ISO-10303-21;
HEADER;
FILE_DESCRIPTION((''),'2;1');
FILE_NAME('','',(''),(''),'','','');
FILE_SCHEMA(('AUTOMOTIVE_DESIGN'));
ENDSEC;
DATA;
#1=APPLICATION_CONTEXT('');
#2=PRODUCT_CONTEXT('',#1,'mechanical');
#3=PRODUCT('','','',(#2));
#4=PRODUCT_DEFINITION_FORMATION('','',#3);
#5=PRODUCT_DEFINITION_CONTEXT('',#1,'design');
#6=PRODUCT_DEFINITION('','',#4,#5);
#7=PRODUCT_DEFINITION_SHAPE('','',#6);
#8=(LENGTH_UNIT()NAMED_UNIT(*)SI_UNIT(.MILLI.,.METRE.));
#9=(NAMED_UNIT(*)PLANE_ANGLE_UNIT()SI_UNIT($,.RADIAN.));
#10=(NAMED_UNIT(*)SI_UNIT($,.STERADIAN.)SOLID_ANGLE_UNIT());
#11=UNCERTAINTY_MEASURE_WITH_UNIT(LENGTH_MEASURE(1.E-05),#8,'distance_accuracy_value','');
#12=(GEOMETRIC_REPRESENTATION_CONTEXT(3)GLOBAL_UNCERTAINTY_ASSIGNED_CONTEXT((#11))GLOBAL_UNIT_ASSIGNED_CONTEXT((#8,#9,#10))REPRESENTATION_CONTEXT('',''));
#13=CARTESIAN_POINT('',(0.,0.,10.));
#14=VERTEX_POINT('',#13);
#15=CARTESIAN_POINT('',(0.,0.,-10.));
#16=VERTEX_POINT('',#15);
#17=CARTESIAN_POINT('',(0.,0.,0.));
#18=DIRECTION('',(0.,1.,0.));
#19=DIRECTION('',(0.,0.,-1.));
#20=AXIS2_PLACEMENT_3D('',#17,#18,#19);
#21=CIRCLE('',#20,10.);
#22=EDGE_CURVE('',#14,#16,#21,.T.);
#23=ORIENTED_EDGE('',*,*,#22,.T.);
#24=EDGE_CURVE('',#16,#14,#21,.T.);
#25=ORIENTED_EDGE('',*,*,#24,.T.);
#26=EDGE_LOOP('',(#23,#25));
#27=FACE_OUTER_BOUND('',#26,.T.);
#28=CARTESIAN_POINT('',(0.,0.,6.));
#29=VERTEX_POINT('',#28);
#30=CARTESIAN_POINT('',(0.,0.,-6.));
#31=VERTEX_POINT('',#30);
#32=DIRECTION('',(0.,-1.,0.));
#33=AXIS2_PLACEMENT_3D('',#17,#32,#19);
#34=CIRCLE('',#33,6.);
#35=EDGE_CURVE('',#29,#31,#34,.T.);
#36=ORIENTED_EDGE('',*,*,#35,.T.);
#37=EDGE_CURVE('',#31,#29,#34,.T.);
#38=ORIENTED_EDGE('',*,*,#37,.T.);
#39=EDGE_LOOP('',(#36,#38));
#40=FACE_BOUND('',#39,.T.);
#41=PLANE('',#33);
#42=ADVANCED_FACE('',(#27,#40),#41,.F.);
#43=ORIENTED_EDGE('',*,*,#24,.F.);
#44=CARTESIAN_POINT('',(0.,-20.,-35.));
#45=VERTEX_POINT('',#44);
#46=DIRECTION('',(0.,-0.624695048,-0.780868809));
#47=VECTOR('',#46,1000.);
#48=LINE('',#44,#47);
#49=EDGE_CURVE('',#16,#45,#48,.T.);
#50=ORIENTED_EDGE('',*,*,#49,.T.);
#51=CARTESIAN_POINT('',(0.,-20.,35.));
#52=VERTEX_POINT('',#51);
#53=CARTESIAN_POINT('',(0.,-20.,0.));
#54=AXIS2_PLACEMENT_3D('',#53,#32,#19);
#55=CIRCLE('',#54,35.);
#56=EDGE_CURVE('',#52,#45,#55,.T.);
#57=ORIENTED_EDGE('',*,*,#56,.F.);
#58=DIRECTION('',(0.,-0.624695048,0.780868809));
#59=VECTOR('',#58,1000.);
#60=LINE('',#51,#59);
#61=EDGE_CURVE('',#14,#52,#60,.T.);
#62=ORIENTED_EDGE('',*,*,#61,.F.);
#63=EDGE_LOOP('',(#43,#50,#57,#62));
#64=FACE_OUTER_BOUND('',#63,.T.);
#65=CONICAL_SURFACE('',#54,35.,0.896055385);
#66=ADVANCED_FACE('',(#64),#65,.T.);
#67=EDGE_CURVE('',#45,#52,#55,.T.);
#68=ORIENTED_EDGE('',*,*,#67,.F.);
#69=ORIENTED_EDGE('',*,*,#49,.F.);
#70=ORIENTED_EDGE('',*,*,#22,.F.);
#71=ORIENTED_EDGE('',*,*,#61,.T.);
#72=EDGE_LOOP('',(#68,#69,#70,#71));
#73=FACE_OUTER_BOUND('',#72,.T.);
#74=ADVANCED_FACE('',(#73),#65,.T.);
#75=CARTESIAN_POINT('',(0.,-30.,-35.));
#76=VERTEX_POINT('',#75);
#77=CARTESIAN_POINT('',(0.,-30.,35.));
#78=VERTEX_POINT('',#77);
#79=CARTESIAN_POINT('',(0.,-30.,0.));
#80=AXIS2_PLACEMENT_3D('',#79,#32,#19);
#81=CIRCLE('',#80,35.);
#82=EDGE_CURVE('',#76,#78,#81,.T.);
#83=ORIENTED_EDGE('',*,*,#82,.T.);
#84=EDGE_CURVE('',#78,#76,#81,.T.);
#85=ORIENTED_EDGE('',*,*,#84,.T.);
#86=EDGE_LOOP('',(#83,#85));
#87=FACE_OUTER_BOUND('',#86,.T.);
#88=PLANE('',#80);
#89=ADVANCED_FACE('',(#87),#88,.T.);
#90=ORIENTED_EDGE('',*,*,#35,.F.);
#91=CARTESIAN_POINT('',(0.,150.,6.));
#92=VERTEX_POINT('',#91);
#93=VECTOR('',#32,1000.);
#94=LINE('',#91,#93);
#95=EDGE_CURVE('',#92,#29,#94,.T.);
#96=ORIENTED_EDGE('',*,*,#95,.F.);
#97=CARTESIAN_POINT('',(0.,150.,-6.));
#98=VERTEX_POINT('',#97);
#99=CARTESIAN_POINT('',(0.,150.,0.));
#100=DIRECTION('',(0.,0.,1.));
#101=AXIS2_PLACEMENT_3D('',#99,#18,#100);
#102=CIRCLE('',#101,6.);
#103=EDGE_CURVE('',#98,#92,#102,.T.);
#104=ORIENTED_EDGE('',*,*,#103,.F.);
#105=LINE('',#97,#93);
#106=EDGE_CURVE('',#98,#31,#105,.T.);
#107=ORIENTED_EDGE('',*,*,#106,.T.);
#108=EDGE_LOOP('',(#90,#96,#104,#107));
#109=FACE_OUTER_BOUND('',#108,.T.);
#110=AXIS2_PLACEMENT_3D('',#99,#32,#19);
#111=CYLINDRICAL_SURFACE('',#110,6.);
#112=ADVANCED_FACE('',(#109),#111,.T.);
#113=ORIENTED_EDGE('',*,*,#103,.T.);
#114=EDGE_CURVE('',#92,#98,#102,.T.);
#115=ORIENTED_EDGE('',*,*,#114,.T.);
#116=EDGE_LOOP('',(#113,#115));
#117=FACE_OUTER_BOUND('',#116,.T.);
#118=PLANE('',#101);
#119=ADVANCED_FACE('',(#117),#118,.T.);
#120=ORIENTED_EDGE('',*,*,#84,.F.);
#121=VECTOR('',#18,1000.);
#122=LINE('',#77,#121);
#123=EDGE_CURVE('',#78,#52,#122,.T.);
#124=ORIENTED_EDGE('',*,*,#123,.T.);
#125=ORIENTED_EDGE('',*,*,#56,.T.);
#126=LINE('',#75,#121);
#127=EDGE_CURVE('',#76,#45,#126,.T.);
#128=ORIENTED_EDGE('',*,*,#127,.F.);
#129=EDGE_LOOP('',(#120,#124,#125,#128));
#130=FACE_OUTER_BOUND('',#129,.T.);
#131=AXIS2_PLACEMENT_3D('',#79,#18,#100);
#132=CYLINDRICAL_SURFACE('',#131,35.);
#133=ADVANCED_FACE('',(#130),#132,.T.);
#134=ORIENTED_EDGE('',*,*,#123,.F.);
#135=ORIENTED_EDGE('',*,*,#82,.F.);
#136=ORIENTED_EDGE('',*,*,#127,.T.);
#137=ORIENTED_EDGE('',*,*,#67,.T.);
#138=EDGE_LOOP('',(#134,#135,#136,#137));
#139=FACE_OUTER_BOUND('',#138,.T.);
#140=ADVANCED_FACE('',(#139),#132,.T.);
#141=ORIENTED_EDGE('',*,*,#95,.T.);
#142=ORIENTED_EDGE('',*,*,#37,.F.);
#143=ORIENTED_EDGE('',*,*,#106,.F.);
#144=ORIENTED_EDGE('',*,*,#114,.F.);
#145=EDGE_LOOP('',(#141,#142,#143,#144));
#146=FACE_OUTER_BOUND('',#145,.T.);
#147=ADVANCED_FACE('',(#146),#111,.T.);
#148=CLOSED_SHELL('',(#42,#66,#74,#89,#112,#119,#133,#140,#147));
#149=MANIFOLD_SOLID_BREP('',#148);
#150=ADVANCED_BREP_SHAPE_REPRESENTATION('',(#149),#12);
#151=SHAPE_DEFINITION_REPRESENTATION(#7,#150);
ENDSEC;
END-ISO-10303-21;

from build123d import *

# Parameters (mm, degrees)
SKETCH_1_R      = 6
EXTRUDE_1_DEPTH = 150
SKETCH_2_R      = 35
EXTRUDE_2_DEPTH = 30
CHAMFER_1_SIZE  = 25
CHAMFER_1_SIZE2 = 20


with BuildPart() as part:
    # 草图1 → 凸台-拉伸1 (new body)
    with BuildSketch(Plane(origin=(0, 0, 0), x_dir=(1, 0, 0), z_dir=(0, 1, 0))):
        with Locations(Location((0, 0, 0), (0, 0, 270))):
            Circle(SKETCH_1_R)
    extrude(amount=EXTRUDE_1_DEPTH)

    # 草图2 → 凸台-拉伸2 (add)
    with BuildSketch(Plane.XZ):
        with Locations(Location((0, 0, 0), (0, 0, 270))):
            Circle(SKETCH_2_R)
    extrude(amount=EXTRUDE_2_DEPTH)

    # 倒角1
    chamfer_1_edges = [part.edges().sort_by_distance(p)[0] for p in [
        (0, 0, 35),
    ]]
    chamfer_1_side = [part.faces().sort_by_distance(p)[0] for p in [
        (0, 0, 34.010050506),
    ]]
    chamfer(chamfer_1_edges, length=CHAMFER_1_SIZE, length2=CHAMFER_1_SIZE2, reference=chamfer_1_side[0])


solid = part.part
